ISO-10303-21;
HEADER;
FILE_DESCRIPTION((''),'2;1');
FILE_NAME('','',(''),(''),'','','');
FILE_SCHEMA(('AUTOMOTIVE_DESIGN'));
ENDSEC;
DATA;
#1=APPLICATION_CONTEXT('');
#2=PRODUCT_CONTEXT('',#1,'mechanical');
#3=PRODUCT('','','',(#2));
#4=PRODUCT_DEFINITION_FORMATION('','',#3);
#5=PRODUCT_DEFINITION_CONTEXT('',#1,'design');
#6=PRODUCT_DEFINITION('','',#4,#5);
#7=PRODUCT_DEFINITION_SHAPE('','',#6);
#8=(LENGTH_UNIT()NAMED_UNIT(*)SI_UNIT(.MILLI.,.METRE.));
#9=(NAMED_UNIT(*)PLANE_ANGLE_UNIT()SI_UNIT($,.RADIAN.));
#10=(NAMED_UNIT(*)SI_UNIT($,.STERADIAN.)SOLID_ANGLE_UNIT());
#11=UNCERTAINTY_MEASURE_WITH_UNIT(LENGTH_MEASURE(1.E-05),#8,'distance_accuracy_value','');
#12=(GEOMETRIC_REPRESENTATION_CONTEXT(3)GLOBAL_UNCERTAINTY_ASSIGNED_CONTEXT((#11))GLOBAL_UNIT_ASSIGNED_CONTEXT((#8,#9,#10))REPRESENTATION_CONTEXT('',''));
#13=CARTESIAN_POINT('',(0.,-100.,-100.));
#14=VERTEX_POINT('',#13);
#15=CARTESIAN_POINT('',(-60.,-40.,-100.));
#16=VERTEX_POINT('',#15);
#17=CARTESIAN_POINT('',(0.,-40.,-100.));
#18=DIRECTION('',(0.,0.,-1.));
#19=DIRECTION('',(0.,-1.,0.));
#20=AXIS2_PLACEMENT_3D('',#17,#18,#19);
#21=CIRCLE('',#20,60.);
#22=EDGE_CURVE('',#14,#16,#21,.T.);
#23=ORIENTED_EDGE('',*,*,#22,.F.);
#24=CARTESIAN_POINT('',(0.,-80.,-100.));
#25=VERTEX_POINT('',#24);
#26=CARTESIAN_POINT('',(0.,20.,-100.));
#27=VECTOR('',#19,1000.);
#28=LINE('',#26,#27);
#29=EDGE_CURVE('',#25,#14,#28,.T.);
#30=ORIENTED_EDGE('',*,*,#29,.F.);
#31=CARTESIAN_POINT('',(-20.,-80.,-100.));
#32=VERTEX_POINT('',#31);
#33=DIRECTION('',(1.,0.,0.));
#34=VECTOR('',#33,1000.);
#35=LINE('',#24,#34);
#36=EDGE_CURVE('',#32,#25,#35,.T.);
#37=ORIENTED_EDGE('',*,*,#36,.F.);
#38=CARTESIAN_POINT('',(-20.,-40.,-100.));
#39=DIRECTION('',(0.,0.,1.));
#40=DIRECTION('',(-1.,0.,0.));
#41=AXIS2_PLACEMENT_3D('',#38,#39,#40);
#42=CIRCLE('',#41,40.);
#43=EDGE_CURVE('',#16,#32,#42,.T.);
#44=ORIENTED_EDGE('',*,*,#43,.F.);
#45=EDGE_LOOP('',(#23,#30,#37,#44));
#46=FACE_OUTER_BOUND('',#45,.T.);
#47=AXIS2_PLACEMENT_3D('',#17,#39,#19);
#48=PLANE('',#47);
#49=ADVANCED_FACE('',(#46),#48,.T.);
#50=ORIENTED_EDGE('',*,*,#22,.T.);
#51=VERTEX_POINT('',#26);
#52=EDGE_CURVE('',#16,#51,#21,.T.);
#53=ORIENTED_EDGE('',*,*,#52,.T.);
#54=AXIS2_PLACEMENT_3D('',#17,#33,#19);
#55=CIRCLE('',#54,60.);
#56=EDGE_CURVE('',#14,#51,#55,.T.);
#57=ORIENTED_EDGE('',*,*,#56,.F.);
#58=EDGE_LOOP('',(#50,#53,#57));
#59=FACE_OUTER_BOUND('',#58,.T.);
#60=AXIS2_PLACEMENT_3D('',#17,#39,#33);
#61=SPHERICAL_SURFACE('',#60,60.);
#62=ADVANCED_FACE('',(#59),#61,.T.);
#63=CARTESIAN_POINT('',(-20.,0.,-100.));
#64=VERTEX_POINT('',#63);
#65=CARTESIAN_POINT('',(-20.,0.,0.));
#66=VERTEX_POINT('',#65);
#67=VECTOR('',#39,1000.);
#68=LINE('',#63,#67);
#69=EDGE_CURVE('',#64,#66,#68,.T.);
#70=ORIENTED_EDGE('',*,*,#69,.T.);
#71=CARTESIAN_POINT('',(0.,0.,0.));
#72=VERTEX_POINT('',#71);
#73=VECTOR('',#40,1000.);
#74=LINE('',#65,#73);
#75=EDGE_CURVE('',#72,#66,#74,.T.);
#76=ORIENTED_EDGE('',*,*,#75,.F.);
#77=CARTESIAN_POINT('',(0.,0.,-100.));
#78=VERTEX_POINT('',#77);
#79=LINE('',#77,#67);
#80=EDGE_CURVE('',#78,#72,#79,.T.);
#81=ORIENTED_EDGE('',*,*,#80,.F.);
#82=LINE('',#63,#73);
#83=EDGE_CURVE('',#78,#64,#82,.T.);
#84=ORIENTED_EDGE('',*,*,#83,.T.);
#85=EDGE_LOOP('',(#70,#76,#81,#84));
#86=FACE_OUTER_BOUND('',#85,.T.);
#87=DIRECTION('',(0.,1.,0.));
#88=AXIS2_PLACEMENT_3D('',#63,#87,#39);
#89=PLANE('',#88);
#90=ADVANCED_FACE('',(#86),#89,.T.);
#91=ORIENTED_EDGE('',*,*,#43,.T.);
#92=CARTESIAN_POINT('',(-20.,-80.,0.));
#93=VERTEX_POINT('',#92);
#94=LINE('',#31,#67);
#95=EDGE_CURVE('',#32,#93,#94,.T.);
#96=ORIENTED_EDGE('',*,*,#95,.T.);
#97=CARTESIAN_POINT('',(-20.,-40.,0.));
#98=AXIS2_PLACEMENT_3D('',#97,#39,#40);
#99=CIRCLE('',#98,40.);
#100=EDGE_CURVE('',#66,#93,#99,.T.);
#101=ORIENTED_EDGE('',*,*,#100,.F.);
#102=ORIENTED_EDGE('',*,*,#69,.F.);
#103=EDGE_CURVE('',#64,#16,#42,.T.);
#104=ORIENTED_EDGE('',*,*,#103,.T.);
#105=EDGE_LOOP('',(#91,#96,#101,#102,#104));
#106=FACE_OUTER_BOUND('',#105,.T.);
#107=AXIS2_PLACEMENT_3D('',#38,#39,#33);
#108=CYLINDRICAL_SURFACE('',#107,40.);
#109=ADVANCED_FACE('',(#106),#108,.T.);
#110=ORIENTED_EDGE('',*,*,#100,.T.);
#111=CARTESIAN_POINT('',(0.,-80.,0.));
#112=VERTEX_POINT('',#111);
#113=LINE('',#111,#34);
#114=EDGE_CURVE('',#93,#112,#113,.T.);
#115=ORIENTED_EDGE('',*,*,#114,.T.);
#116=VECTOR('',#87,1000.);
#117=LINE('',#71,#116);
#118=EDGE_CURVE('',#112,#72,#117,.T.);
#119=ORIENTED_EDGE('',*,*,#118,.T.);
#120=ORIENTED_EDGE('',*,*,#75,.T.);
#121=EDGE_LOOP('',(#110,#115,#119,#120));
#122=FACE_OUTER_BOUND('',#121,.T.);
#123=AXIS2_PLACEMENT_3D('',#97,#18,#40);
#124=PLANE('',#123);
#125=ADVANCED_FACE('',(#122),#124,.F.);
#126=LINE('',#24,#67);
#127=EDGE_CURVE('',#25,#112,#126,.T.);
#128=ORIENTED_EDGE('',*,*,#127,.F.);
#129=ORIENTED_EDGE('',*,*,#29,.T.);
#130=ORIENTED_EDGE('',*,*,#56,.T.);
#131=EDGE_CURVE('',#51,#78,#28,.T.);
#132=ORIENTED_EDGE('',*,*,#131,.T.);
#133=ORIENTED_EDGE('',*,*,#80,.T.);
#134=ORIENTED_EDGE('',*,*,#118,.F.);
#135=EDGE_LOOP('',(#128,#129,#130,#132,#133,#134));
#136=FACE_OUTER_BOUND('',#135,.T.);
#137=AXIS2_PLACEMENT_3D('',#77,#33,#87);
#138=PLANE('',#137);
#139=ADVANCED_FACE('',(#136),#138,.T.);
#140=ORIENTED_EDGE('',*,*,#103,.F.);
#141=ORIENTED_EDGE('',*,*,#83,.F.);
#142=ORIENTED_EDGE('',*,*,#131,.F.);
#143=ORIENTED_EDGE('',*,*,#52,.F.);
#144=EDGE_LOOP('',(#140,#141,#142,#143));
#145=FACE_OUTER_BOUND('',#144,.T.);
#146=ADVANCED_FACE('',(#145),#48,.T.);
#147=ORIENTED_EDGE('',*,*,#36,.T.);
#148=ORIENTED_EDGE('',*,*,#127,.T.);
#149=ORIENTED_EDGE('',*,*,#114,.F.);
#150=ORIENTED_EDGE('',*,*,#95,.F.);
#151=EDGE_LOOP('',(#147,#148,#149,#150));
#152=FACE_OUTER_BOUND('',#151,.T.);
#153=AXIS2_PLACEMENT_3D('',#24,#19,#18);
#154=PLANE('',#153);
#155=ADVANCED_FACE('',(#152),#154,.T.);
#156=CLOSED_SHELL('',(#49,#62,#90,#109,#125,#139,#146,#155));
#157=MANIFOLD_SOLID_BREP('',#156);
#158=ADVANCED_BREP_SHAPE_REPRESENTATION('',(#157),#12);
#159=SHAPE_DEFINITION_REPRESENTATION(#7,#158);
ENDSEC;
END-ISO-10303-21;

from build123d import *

# Parameters (mm, degrees)
EXTRUDE_1_DEPTH = 100
REVOLVE_1_ANGLE = 90


with BuildPart() as part:
    # 草图1 → 凸台-拉伸1 (new body)
    with BuildSketch(Plane.XY):
        with BuildLine():
            Line((0, 0), (0, -80))
            Line((0, -80), (-20, -80))
            ThreePointArc((-20, -80), (-60, -40), (-20, 0))
            Line((-20, 0), (0, 0))
        make_face()
    extrude(amount=-EXTRUDE_1_DEPTH)

    # 草图2 → 旋转1 (revolve)
    with BuildSketch(Plane(origin=(0, 0, 0), x_dir=(0, 0, -1), z_dir=(1, 0, 0))):
        with BuildLine():
            Line((100, 20), (100, -100))
            ThreePointArc((100, -100), (160, -40), (100, 20))
        make_face()
    revolve(axis=Axis((0, 20, -100), (0, 1, 0)), revolution_arc=REVOLVE_1_ANGLE)


solid = part.part
